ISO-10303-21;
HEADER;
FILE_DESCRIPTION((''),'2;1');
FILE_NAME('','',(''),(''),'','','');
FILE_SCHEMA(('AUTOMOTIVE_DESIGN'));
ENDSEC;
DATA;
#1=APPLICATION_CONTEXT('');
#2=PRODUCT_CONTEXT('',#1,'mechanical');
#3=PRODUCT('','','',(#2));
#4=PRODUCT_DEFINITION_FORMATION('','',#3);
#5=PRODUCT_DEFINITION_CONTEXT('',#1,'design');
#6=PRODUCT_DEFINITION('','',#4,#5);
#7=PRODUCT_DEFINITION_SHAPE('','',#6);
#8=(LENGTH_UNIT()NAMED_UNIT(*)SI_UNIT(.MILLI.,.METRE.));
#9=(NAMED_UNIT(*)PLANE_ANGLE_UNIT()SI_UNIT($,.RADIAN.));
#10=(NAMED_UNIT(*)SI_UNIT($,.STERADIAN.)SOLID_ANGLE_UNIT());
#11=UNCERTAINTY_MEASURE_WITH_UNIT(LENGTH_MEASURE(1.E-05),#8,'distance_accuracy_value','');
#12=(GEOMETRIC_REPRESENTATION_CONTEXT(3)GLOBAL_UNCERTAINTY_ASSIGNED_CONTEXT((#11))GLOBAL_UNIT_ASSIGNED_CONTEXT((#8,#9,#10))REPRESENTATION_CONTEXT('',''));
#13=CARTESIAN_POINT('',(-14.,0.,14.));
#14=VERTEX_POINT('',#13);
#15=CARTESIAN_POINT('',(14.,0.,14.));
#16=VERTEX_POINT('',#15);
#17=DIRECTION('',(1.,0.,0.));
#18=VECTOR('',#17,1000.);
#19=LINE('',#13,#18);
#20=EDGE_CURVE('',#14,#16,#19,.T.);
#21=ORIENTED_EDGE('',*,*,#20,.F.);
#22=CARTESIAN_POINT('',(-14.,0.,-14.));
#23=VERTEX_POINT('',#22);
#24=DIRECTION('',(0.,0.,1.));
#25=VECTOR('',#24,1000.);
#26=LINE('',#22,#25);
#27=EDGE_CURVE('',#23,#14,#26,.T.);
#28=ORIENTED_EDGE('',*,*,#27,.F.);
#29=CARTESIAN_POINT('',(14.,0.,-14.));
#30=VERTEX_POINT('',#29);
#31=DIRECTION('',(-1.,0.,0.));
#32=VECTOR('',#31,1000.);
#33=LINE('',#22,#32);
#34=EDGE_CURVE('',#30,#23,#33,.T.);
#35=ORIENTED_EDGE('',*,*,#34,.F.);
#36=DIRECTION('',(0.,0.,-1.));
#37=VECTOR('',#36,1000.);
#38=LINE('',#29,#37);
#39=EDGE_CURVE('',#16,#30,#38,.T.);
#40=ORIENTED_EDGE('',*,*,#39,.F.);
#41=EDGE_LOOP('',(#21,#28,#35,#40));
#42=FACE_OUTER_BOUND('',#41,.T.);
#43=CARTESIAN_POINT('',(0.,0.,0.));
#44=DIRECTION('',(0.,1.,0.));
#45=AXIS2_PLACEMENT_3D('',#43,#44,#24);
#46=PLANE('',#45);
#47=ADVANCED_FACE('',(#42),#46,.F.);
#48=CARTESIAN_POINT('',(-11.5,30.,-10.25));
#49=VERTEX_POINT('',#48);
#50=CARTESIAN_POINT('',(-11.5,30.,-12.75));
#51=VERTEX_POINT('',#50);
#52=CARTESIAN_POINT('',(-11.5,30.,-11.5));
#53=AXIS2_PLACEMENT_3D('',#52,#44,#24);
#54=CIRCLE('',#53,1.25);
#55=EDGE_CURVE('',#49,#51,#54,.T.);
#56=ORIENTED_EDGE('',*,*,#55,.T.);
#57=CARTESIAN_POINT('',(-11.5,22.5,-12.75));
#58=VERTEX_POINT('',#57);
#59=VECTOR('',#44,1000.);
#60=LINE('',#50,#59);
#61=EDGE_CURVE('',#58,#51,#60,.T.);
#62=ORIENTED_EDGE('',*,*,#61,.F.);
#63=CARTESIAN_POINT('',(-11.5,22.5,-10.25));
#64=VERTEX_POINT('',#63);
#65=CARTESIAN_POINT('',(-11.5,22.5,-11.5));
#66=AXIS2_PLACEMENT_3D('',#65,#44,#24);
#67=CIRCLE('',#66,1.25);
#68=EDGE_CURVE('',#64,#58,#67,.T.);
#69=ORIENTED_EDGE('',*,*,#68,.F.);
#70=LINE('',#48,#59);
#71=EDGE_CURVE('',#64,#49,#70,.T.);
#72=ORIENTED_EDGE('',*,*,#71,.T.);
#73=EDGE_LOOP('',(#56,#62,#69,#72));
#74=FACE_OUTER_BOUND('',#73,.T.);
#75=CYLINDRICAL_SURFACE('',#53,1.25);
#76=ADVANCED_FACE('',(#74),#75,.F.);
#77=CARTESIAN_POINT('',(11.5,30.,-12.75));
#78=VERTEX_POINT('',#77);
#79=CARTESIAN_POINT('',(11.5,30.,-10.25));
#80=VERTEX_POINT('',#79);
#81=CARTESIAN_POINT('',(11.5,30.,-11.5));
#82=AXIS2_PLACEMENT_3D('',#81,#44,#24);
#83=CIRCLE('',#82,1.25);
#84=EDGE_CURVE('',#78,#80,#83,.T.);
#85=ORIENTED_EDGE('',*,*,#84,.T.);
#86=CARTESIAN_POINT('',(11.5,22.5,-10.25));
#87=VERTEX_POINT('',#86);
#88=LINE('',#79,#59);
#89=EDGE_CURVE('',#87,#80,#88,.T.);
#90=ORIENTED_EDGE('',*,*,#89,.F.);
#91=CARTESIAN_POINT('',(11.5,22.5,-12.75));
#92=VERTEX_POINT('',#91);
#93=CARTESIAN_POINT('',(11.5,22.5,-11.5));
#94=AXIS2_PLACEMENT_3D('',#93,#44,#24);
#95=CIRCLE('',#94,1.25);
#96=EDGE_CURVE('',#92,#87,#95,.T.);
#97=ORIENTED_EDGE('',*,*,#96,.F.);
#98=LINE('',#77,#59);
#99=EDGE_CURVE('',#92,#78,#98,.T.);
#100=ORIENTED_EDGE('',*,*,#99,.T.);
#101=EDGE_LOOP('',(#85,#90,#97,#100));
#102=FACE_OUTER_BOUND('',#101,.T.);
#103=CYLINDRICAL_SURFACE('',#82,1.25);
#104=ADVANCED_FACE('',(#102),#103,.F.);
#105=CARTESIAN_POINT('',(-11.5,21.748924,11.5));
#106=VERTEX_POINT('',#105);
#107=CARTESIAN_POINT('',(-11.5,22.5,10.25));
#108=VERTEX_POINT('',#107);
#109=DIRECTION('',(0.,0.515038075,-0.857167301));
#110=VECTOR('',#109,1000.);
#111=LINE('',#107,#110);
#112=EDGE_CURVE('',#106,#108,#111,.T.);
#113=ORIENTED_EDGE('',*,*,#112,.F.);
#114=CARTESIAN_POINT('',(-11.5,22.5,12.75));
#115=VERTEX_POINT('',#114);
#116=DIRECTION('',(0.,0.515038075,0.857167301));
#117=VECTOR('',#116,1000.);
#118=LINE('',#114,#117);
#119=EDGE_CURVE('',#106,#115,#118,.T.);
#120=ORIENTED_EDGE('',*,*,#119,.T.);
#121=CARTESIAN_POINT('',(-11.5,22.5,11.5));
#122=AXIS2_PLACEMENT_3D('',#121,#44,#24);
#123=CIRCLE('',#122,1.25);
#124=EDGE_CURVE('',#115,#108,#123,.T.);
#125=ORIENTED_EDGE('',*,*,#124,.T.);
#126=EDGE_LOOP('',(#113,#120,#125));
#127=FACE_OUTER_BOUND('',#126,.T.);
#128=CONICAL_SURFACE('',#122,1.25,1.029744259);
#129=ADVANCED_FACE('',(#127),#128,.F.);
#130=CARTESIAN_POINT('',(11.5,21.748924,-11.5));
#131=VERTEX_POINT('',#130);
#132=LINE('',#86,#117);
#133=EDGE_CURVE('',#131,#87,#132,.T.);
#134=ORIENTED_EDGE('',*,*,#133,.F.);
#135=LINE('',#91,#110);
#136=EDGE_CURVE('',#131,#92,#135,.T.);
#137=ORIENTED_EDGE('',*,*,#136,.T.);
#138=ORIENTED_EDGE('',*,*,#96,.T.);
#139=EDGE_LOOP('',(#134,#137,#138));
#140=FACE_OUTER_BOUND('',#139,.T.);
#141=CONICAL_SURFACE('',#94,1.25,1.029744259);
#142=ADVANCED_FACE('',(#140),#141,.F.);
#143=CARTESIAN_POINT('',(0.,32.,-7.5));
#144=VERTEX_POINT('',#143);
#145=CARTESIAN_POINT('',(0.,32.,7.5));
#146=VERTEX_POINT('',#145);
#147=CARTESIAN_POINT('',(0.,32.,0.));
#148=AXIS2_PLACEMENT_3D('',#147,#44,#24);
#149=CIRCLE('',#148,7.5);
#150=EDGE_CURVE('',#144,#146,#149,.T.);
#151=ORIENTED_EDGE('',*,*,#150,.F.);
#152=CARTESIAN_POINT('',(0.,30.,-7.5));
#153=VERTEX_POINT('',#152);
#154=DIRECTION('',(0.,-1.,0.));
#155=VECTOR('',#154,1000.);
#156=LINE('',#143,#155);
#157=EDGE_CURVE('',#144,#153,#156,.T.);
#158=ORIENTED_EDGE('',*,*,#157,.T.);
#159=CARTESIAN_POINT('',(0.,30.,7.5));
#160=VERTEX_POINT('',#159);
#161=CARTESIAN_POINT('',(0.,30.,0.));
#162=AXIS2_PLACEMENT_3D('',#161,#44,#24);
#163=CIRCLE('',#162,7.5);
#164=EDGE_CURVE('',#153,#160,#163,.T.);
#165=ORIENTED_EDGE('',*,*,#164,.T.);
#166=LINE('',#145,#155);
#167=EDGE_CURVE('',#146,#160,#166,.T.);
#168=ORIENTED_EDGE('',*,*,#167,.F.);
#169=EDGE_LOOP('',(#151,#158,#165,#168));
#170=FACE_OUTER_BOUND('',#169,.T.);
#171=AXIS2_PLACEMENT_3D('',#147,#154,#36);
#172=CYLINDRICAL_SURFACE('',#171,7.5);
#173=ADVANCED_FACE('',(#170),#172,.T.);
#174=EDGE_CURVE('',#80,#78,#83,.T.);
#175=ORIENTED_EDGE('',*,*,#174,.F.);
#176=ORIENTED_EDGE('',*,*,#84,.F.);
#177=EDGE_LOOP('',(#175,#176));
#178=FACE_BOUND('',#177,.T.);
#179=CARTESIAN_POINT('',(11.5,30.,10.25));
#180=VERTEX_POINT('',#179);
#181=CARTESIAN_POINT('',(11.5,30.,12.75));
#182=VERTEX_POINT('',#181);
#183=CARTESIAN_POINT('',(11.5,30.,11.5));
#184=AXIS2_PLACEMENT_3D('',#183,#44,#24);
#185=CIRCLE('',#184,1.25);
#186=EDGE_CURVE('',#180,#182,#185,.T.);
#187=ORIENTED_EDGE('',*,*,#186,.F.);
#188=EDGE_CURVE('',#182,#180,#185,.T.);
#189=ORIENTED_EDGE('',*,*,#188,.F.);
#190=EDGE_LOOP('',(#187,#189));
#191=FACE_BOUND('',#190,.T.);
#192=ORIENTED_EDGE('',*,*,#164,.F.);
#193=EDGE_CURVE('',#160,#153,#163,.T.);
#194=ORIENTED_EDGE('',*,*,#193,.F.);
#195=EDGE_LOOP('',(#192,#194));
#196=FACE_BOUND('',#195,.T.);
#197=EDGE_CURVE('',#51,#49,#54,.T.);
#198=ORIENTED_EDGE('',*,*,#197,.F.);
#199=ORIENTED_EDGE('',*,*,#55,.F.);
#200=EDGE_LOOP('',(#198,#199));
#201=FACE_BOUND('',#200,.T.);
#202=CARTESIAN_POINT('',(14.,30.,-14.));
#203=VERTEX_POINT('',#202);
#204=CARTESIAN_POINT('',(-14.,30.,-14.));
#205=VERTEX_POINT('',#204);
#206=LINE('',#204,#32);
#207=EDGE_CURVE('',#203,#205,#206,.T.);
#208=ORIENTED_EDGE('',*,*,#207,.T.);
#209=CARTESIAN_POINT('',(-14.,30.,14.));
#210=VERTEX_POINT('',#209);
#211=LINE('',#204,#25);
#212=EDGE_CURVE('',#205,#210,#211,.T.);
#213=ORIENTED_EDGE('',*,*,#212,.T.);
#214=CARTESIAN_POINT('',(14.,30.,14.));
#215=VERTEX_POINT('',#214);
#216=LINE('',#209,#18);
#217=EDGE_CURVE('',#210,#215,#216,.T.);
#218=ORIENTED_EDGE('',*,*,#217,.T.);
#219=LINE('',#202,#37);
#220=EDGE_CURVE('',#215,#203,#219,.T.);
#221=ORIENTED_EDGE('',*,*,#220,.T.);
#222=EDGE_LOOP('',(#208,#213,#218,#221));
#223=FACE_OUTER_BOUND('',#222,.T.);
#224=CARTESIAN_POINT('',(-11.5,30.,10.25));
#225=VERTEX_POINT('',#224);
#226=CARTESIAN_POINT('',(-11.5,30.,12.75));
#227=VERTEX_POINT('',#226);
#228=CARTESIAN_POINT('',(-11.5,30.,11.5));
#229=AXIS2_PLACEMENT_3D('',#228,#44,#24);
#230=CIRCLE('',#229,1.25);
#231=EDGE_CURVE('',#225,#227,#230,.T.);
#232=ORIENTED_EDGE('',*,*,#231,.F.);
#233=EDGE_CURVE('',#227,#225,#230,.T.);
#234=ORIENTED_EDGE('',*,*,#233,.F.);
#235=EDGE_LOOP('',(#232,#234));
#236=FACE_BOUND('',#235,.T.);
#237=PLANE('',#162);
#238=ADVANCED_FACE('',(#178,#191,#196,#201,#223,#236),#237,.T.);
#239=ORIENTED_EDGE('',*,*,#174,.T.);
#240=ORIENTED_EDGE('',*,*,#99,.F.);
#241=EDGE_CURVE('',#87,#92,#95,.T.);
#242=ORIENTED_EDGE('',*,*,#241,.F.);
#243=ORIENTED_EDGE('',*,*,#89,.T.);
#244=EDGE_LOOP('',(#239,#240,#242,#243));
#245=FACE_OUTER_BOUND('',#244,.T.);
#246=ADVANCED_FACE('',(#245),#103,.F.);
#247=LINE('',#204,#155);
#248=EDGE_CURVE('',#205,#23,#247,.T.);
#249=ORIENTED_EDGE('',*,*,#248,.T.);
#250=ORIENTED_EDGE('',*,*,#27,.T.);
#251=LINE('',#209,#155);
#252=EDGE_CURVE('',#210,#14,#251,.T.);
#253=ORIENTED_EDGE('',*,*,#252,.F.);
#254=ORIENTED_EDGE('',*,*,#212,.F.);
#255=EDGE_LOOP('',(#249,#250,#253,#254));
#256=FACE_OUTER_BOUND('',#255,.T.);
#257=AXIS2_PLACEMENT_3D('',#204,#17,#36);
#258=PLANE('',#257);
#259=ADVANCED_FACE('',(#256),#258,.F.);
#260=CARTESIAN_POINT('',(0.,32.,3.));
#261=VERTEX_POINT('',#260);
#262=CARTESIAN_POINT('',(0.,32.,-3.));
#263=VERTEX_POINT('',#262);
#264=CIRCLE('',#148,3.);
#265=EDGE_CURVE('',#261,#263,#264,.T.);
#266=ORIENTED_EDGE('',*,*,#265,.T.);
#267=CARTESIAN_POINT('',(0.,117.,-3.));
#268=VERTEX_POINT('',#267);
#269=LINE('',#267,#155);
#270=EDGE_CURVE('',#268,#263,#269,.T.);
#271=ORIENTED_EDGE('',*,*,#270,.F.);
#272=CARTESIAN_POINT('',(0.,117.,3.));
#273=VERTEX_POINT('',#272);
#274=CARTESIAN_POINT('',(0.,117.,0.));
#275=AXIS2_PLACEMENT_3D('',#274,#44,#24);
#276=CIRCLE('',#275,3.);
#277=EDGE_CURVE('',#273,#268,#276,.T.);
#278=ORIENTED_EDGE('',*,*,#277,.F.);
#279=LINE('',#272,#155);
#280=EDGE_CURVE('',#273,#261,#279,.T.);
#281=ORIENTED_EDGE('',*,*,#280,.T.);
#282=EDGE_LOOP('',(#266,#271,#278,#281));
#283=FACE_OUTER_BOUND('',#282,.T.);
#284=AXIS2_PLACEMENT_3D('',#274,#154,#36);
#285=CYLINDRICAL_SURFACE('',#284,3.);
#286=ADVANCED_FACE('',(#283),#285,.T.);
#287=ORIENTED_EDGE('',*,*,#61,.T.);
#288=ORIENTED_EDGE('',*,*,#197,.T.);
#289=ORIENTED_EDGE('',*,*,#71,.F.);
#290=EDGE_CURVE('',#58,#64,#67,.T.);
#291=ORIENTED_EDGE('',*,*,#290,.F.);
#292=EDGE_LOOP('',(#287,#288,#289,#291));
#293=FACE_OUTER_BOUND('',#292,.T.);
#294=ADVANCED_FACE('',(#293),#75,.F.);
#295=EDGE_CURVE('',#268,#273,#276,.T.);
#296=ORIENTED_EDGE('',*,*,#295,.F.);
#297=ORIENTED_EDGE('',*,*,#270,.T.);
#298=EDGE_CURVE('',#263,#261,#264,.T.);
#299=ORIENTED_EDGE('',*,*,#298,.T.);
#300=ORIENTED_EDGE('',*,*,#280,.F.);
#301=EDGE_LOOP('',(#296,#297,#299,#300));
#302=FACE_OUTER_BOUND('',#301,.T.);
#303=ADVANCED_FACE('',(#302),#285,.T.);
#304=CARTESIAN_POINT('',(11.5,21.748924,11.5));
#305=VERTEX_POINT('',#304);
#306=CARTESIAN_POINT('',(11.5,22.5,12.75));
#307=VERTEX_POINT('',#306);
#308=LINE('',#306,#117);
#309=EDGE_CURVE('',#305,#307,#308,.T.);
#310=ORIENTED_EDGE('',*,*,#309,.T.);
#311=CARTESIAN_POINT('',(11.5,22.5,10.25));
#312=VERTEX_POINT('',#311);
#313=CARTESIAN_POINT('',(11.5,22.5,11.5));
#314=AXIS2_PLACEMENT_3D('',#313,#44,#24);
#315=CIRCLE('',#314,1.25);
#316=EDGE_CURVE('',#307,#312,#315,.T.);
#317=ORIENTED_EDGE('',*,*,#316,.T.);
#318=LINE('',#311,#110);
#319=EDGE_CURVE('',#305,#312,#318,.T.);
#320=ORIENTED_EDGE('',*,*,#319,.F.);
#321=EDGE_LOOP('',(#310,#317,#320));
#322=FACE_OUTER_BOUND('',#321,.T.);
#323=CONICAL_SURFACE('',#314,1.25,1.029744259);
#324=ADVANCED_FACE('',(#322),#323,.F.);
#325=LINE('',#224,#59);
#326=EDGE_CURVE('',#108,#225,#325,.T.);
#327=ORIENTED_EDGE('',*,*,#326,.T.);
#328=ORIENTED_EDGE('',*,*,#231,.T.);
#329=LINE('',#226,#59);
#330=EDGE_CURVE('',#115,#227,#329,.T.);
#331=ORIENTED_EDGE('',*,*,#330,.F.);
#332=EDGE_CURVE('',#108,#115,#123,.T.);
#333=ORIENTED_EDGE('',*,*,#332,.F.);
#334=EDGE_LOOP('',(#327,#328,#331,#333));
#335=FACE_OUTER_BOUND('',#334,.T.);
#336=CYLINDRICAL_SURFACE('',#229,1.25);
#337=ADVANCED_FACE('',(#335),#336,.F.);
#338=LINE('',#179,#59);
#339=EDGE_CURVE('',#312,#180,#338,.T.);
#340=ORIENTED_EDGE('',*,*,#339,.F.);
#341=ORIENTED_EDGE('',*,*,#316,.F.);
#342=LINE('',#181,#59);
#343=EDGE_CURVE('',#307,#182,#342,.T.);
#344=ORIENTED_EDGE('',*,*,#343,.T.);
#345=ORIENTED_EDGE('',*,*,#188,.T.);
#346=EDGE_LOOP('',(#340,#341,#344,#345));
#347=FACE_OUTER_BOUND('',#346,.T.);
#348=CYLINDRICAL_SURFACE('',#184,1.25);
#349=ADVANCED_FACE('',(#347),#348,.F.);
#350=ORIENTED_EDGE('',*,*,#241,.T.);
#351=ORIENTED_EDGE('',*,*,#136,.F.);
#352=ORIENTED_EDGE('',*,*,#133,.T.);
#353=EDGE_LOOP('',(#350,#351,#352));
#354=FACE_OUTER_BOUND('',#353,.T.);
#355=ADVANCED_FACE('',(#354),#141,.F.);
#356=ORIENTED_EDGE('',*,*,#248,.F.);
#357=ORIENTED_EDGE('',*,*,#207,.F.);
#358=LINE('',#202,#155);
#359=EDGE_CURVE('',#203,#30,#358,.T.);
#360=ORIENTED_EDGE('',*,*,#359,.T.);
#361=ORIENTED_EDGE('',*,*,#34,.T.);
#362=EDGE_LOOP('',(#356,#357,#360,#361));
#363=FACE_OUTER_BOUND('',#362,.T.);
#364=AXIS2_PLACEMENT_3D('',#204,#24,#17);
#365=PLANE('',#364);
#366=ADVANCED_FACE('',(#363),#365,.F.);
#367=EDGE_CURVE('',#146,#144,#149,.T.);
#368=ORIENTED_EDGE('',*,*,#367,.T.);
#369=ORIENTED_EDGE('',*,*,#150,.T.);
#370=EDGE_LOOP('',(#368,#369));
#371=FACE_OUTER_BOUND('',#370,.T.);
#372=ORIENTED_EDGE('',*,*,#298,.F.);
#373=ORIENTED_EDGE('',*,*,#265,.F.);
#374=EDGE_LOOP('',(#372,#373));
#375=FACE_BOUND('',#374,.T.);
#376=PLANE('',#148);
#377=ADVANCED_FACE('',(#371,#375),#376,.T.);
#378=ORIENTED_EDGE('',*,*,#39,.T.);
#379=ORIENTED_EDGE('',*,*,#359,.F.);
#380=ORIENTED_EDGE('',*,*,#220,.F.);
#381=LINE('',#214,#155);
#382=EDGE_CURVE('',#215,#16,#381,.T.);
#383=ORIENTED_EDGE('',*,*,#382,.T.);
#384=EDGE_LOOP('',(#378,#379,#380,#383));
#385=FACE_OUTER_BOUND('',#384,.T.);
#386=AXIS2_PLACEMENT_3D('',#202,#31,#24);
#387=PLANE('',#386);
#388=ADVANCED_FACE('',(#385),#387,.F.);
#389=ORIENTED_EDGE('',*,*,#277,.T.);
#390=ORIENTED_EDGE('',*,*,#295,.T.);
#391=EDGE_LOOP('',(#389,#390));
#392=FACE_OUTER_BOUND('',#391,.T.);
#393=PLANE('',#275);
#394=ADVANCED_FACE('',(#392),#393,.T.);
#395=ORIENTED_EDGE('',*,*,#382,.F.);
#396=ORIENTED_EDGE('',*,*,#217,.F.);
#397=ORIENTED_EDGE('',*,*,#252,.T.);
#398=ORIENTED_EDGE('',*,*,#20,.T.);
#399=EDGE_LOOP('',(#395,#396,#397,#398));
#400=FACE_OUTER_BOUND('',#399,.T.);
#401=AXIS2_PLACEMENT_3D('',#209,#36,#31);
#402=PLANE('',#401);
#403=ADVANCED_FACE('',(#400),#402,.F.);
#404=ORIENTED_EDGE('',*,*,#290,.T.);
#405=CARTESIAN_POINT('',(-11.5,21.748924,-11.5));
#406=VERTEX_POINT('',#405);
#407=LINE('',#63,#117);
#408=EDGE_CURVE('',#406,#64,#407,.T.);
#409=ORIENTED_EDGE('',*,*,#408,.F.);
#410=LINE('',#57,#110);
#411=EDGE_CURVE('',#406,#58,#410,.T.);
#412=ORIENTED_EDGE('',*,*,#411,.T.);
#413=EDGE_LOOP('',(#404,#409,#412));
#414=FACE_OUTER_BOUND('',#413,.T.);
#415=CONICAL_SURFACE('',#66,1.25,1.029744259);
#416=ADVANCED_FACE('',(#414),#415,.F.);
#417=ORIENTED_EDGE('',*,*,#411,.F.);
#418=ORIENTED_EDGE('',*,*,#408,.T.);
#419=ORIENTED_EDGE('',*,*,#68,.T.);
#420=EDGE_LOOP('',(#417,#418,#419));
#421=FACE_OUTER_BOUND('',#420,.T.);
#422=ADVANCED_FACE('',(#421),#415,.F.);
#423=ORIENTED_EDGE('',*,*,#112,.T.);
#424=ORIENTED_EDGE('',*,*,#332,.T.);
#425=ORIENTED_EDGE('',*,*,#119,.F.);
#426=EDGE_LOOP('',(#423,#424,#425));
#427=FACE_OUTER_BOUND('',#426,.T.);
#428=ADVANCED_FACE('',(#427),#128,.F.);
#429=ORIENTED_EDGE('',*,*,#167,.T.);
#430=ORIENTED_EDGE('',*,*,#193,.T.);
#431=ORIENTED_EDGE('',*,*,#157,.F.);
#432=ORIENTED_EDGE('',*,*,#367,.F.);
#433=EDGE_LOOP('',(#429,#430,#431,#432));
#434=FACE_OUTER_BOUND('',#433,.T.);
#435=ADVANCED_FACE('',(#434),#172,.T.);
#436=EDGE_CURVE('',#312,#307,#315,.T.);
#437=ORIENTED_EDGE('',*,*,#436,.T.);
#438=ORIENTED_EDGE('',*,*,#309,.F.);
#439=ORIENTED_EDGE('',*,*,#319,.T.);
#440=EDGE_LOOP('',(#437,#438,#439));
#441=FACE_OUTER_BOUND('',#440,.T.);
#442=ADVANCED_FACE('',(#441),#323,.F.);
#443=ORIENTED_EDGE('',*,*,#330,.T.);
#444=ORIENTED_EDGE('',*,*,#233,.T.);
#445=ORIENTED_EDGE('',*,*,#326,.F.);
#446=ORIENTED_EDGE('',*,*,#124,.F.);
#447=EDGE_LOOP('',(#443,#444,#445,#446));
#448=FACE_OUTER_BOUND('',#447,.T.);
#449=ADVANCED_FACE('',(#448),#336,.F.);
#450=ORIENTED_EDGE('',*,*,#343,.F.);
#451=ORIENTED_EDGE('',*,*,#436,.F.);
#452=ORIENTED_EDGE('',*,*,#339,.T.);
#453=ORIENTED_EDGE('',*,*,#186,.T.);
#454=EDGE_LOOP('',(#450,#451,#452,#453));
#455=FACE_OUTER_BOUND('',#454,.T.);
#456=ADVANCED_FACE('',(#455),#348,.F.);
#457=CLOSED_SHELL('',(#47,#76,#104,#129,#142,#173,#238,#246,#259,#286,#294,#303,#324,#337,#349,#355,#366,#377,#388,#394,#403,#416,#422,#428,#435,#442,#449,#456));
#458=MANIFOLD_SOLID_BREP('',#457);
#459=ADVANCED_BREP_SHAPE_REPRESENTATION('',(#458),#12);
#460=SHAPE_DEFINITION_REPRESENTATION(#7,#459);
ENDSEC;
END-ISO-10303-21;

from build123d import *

# Parameters (mm, degrees)
SKETCH1_W             = 28
SKETCH1_H             = 28
BOSS_EXTRUDE1_DEPTH   = 30
SKETCH2_R             = 7.5
BOSS_EXTRUDE2_DEPTH   = 2
SKETCH3_R             = 3
BOSS_EXTRUDE3_DEPTH   = 85
SKETCH4_R             = 1
CUT_EXTRUDE1_DEPTH    = 3
M3_TAPPED_HOLE1_D     = 2.5
M3_TAPPED_HOLE1_DEPTH = 7.5
M3_TAPPED_HOLE1_TIP   = 0.751075774


with BuildPart() as part:
    # Sketch1 → Boss-Extrude1 (new body)
    with BuildSketch(Plane(origin=(0, 0, 0), x_dir=(1, 0, 0), z_dir=(0, 1, 0))):
        Rectangle(SKETCH1_W, SKETCH1_H)
    extrude(amount=BOSS_EXTRUDE1_DEPTH)

    # Sketch2 → Boss-Extrude2 (add)
    with BuildSketch(Plane(origin=(0, 30, 0), x_dir=(1, 0, 0), z_dir=(0, 1, 0))):
        with Locations(Location((0, 0, 0), (0, 0, 270))):
            Circle(SKETCH2_R)
    extrude(amount=BOSS_EXTRUDE2_DEPTH)

    # Sketch3 → Boss-Extrude3 (add)
    with BuildSketch(Plane(origin=(0, 32, 0), x_dir=(1, 0, 0), z_dir=(0, 1, 0))):
        with Locations(Location((0, 0, 0), (0, 0, 270))):
            Circle(SKETCH3_R)
    extrude(amount=BOSS_EXTRUDE3_DEPTH)

    # Sketch4 → Cut-Extrude1 (cut)
    with BuildSketch(Plane(origin=(0, 30, 0), x_dir=(1, 0, 0), z_dir=(0, 1, 0))):
        with Locations(Location((-11.5, -11.5, 0), (0, 0, 270))):
            Circle(SKETCH4_R)
        with Locations(Location((11.5, -11.5, 0), (0, 0, 270))):
            Circle(SKETCH4_R)
        with Locations(Location((-11.5, 11.5, 0), (0, 0, 270))):
            Circle(SKETCH4_R)
        with Locations(Location((11.5, 11.5, 0), (0, 0, 270))):
            Circle(SKETCH4_R)
    extrude(amount=-CUT_EXTRUDE1_DEPTH, mode=Mode.SUBTRACT)

    # M3 Tapped Hole1
    with Locations(Plane(origin=(0, 30, 0), x_dir=(1, 0, 0), z_dir=(0, 1, 0))):
        with Locations((-11.5, -11.5), (11.5, -11.5), (-11.5, 11.5), (11.5, 11.5)):
            Hole(M3_TAPPED_HOLE1_D / 2, depth=M3_TAPPED_HOLE1_DEPTH)
            with Locations((0, 0, -(M3_TAPPED_HOLE1_DEPTH + M3_TAPPED_HOLE1_TIP / 2))):  # 118° drill point
                Cone(0, M3_TAPPED_HOLE1_D / 2, M3_TAPPED_HOLE1_TIP, mode=Mode.SUBTRACT)


solid = part.part
